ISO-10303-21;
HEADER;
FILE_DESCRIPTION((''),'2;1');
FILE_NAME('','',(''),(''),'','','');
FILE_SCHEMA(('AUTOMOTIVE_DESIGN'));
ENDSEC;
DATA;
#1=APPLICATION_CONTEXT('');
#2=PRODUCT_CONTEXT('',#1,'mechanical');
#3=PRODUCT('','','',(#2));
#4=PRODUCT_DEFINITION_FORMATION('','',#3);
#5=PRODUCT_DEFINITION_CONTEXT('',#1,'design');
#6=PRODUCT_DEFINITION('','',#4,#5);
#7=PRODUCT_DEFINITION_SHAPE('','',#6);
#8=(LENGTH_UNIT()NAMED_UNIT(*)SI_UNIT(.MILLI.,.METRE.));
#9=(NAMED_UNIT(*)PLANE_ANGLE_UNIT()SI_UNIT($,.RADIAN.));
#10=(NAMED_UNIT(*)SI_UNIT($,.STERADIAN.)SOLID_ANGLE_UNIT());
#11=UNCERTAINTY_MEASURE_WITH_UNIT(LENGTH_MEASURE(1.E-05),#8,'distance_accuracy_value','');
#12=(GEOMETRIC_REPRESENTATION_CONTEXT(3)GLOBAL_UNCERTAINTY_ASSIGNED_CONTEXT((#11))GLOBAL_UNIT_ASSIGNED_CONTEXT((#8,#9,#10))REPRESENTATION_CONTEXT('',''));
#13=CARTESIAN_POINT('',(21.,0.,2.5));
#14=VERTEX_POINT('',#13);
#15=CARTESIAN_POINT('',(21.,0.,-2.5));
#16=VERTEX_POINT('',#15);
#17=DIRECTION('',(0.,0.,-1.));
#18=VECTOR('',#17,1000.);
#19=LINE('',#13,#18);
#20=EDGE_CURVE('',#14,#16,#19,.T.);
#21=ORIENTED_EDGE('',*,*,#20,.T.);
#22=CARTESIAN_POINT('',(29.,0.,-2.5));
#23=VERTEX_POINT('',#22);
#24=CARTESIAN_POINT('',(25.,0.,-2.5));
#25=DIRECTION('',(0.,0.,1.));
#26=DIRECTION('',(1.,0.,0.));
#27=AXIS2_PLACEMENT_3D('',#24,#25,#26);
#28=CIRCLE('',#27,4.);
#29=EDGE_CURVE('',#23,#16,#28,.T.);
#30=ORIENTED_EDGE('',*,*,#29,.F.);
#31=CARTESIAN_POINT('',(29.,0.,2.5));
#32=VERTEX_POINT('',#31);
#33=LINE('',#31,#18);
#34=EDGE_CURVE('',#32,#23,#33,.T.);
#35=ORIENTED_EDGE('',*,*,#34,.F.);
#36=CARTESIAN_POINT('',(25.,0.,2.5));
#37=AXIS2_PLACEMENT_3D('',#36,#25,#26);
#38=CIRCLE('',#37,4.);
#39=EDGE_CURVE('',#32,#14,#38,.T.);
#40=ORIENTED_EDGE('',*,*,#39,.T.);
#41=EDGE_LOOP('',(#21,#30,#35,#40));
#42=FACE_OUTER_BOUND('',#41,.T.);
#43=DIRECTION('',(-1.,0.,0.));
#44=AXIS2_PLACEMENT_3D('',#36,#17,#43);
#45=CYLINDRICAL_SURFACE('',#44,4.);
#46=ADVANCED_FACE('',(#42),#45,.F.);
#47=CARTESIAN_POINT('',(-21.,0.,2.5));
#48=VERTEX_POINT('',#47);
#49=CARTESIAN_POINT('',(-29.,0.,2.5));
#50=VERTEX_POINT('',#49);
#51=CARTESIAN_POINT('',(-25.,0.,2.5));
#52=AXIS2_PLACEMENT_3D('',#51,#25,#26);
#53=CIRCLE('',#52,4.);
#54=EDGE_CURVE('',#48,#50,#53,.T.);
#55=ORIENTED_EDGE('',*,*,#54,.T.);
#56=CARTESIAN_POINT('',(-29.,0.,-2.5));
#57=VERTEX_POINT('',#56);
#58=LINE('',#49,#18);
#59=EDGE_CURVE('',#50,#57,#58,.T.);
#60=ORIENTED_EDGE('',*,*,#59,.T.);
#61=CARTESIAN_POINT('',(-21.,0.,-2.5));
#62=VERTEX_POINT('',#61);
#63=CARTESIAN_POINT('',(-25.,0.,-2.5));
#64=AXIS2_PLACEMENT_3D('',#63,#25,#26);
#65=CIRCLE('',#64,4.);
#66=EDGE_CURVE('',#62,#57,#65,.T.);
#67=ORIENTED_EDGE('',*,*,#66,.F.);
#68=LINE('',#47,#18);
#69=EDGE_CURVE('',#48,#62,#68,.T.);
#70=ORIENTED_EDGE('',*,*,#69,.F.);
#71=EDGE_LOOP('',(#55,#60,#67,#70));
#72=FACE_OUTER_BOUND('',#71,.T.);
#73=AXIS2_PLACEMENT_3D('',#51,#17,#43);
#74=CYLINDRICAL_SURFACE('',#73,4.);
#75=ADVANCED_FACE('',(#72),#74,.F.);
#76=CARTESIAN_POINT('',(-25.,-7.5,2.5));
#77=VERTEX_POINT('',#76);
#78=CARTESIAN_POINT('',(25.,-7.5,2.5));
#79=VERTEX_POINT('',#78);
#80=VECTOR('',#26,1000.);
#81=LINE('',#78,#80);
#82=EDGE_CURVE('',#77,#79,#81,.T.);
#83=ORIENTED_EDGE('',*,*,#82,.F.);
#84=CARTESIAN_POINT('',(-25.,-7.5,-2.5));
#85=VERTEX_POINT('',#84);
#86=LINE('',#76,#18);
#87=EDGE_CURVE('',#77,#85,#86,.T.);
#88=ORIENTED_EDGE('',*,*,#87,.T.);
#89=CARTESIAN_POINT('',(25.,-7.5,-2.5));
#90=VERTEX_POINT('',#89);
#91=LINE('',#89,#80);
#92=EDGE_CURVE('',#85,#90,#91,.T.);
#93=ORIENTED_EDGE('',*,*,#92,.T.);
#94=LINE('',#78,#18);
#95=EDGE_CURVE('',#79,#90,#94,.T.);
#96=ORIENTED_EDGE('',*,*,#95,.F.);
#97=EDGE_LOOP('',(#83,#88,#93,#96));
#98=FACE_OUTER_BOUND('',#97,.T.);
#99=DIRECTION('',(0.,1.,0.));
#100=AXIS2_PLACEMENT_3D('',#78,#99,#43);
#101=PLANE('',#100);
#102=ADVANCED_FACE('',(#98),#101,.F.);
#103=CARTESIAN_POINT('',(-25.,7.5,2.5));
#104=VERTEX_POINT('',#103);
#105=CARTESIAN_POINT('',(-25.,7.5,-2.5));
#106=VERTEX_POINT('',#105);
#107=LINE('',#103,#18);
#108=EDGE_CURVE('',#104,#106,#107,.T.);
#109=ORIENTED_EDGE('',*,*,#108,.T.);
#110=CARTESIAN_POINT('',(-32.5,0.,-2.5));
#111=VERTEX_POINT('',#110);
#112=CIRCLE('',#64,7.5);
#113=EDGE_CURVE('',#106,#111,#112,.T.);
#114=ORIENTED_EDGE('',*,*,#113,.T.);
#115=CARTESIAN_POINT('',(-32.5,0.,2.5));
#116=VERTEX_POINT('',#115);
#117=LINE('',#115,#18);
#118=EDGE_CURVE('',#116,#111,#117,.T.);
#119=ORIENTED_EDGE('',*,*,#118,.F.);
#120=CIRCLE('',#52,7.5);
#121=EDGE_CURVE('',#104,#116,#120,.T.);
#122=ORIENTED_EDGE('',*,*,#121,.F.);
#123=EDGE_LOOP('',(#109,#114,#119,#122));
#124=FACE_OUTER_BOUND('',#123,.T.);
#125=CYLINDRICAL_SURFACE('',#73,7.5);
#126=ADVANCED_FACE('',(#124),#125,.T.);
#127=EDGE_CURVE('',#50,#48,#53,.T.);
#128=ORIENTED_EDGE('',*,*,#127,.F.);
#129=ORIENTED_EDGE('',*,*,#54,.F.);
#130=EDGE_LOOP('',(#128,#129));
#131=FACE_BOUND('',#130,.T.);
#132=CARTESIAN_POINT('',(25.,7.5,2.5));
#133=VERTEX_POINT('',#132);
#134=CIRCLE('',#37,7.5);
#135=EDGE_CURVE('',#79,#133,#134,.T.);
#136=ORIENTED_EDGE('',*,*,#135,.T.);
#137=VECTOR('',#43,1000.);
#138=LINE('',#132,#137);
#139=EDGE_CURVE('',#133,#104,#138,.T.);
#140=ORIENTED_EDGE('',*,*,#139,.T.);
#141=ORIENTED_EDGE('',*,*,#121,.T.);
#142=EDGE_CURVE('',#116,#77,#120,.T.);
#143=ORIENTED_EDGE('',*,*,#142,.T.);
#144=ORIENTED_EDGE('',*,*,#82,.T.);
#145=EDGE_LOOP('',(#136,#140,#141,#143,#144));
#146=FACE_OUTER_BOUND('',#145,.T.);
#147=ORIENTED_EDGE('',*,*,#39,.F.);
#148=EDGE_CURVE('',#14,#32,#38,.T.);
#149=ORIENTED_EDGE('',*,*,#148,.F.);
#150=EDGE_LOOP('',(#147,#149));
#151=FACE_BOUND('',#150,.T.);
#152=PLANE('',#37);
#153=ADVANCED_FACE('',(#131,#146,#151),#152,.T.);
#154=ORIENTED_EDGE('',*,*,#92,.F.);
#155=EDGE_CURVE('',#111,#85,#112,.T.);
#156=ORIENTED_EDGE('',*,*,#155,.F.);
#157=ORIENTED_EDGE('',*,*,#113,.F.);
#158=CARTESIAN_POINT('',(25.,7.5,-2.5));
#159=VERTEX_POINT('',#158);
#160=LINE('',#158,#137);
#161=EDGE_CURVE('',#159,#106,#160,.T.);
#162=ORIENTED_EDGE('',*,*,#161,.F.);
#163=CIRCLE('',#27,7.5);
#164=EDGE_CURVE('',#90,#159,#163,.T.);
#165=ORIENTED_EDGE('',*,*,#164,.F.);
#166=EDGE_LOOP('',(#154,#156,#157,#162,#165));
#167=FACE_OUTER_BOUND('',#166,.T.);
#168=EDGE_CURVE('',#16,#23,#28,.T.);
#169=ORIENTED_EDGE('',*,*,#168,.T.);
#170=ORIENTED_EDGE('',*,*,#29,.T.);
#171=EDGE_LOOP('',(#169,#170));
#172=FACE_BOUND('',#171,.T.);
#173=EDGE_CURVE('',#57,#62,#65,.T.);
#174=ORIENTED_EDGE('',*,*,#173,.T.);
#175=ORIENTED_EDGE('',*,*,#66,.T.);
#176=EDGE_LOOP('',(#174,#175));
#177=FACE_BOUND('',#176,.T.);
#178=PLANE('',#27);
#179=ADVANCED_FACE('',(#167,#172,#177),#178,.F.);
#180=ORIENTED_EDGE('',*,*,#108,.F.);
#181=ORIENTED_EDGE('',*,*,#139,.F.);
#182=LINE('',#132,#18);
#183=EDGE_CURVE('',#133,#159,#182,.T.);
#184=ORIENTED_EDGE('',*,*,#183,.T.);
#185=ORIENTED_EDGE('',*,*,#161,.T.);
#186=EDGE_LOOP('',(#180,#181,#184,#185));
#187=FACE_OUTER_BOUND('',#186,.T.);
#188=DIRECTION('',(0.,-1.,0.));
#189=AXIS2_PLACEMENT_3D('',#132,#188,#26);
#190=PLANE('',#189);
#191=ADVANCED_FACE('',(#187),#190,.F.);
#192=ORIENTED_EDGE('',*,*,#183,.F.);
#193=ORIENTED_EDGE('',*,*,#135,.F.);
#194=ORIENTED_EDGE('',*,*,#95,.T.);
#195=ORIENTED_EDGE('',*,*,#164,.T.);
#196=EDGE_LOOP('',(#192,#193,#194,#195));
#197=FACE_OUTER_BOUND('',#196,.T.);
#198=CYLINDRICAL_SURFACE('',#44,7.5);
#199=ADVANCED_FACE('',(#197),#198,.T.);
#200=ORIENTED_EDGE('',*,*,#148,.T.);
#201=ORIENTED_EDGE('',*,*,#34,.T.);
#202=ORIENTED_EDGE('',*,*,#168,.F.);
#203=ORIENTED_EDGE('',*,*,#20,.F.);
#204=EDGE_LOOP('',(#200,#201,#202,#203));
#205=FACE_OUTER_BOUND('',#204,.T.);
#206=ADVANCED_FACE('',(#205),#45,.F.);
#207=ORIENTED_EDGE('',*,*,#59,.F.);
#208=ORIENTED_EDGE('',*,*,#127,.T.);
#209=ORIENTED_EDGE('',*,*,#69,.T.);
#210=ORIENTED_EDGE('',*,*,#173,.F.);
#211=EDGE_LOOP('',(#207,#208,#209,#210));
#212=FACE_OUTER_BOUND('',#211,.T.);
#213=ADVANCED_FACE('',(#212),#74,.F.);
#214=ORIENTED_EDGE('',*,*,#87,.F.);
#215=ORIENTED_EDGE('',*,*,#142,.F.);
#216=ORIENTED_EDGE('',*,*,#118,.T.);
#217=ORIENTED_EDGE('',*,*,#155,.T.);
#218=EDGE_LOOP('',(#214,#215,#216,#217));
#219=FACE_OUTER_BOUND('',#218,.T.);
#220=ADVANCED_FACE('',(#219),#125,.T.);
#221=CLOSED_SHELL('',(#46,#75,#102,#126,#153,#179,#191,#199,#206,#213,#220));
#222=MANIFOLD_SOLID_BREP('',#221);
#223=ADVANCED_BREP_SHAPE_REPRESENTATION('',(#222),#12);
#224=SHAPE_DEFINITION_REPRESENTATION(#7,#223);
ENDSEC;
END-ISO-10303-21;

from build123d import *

# Parameters (mm, degrees)
LINK_PLATE_PROFILE_SKETCH_R          = 4
LINK_PLATE_5MM_WITH_HOLES_2X_8_DEPTH = 2.5


with BuildPart() as part:
    # Link Plate Profile Sketch → Link Plate 5mm with Holes 2xØ8 (new, symmetric)
    with BuildSketch(Plane.XY):
        with BuildLine():
            Line((25, -7.5), (-25, -7.5))
            ThreePointArc((-25, -7.5), (-32.5, 0), (-25, 7.5))
            Line((-25, 7.5), (25, 7.5))
            ThreePointArc((25, 7.5), (32.5, 0), (25, -7.5))
        make_face()
        with Locations((-25, 0)):
            Circle(LINK_PLATE_PROFILE_SKETCH_R, mode=Mode.SUBTRACT)
        with Locations((25, 0)):
            Circle(LINK_PLATE_PROFILE_SKETCH_R, mode=Mode.SUBTRACT)
    extrude(amount=LINK_PLATE_5MM_WITH_HOLES_2X_8_DEPTH, both=True)


solid = part.part
